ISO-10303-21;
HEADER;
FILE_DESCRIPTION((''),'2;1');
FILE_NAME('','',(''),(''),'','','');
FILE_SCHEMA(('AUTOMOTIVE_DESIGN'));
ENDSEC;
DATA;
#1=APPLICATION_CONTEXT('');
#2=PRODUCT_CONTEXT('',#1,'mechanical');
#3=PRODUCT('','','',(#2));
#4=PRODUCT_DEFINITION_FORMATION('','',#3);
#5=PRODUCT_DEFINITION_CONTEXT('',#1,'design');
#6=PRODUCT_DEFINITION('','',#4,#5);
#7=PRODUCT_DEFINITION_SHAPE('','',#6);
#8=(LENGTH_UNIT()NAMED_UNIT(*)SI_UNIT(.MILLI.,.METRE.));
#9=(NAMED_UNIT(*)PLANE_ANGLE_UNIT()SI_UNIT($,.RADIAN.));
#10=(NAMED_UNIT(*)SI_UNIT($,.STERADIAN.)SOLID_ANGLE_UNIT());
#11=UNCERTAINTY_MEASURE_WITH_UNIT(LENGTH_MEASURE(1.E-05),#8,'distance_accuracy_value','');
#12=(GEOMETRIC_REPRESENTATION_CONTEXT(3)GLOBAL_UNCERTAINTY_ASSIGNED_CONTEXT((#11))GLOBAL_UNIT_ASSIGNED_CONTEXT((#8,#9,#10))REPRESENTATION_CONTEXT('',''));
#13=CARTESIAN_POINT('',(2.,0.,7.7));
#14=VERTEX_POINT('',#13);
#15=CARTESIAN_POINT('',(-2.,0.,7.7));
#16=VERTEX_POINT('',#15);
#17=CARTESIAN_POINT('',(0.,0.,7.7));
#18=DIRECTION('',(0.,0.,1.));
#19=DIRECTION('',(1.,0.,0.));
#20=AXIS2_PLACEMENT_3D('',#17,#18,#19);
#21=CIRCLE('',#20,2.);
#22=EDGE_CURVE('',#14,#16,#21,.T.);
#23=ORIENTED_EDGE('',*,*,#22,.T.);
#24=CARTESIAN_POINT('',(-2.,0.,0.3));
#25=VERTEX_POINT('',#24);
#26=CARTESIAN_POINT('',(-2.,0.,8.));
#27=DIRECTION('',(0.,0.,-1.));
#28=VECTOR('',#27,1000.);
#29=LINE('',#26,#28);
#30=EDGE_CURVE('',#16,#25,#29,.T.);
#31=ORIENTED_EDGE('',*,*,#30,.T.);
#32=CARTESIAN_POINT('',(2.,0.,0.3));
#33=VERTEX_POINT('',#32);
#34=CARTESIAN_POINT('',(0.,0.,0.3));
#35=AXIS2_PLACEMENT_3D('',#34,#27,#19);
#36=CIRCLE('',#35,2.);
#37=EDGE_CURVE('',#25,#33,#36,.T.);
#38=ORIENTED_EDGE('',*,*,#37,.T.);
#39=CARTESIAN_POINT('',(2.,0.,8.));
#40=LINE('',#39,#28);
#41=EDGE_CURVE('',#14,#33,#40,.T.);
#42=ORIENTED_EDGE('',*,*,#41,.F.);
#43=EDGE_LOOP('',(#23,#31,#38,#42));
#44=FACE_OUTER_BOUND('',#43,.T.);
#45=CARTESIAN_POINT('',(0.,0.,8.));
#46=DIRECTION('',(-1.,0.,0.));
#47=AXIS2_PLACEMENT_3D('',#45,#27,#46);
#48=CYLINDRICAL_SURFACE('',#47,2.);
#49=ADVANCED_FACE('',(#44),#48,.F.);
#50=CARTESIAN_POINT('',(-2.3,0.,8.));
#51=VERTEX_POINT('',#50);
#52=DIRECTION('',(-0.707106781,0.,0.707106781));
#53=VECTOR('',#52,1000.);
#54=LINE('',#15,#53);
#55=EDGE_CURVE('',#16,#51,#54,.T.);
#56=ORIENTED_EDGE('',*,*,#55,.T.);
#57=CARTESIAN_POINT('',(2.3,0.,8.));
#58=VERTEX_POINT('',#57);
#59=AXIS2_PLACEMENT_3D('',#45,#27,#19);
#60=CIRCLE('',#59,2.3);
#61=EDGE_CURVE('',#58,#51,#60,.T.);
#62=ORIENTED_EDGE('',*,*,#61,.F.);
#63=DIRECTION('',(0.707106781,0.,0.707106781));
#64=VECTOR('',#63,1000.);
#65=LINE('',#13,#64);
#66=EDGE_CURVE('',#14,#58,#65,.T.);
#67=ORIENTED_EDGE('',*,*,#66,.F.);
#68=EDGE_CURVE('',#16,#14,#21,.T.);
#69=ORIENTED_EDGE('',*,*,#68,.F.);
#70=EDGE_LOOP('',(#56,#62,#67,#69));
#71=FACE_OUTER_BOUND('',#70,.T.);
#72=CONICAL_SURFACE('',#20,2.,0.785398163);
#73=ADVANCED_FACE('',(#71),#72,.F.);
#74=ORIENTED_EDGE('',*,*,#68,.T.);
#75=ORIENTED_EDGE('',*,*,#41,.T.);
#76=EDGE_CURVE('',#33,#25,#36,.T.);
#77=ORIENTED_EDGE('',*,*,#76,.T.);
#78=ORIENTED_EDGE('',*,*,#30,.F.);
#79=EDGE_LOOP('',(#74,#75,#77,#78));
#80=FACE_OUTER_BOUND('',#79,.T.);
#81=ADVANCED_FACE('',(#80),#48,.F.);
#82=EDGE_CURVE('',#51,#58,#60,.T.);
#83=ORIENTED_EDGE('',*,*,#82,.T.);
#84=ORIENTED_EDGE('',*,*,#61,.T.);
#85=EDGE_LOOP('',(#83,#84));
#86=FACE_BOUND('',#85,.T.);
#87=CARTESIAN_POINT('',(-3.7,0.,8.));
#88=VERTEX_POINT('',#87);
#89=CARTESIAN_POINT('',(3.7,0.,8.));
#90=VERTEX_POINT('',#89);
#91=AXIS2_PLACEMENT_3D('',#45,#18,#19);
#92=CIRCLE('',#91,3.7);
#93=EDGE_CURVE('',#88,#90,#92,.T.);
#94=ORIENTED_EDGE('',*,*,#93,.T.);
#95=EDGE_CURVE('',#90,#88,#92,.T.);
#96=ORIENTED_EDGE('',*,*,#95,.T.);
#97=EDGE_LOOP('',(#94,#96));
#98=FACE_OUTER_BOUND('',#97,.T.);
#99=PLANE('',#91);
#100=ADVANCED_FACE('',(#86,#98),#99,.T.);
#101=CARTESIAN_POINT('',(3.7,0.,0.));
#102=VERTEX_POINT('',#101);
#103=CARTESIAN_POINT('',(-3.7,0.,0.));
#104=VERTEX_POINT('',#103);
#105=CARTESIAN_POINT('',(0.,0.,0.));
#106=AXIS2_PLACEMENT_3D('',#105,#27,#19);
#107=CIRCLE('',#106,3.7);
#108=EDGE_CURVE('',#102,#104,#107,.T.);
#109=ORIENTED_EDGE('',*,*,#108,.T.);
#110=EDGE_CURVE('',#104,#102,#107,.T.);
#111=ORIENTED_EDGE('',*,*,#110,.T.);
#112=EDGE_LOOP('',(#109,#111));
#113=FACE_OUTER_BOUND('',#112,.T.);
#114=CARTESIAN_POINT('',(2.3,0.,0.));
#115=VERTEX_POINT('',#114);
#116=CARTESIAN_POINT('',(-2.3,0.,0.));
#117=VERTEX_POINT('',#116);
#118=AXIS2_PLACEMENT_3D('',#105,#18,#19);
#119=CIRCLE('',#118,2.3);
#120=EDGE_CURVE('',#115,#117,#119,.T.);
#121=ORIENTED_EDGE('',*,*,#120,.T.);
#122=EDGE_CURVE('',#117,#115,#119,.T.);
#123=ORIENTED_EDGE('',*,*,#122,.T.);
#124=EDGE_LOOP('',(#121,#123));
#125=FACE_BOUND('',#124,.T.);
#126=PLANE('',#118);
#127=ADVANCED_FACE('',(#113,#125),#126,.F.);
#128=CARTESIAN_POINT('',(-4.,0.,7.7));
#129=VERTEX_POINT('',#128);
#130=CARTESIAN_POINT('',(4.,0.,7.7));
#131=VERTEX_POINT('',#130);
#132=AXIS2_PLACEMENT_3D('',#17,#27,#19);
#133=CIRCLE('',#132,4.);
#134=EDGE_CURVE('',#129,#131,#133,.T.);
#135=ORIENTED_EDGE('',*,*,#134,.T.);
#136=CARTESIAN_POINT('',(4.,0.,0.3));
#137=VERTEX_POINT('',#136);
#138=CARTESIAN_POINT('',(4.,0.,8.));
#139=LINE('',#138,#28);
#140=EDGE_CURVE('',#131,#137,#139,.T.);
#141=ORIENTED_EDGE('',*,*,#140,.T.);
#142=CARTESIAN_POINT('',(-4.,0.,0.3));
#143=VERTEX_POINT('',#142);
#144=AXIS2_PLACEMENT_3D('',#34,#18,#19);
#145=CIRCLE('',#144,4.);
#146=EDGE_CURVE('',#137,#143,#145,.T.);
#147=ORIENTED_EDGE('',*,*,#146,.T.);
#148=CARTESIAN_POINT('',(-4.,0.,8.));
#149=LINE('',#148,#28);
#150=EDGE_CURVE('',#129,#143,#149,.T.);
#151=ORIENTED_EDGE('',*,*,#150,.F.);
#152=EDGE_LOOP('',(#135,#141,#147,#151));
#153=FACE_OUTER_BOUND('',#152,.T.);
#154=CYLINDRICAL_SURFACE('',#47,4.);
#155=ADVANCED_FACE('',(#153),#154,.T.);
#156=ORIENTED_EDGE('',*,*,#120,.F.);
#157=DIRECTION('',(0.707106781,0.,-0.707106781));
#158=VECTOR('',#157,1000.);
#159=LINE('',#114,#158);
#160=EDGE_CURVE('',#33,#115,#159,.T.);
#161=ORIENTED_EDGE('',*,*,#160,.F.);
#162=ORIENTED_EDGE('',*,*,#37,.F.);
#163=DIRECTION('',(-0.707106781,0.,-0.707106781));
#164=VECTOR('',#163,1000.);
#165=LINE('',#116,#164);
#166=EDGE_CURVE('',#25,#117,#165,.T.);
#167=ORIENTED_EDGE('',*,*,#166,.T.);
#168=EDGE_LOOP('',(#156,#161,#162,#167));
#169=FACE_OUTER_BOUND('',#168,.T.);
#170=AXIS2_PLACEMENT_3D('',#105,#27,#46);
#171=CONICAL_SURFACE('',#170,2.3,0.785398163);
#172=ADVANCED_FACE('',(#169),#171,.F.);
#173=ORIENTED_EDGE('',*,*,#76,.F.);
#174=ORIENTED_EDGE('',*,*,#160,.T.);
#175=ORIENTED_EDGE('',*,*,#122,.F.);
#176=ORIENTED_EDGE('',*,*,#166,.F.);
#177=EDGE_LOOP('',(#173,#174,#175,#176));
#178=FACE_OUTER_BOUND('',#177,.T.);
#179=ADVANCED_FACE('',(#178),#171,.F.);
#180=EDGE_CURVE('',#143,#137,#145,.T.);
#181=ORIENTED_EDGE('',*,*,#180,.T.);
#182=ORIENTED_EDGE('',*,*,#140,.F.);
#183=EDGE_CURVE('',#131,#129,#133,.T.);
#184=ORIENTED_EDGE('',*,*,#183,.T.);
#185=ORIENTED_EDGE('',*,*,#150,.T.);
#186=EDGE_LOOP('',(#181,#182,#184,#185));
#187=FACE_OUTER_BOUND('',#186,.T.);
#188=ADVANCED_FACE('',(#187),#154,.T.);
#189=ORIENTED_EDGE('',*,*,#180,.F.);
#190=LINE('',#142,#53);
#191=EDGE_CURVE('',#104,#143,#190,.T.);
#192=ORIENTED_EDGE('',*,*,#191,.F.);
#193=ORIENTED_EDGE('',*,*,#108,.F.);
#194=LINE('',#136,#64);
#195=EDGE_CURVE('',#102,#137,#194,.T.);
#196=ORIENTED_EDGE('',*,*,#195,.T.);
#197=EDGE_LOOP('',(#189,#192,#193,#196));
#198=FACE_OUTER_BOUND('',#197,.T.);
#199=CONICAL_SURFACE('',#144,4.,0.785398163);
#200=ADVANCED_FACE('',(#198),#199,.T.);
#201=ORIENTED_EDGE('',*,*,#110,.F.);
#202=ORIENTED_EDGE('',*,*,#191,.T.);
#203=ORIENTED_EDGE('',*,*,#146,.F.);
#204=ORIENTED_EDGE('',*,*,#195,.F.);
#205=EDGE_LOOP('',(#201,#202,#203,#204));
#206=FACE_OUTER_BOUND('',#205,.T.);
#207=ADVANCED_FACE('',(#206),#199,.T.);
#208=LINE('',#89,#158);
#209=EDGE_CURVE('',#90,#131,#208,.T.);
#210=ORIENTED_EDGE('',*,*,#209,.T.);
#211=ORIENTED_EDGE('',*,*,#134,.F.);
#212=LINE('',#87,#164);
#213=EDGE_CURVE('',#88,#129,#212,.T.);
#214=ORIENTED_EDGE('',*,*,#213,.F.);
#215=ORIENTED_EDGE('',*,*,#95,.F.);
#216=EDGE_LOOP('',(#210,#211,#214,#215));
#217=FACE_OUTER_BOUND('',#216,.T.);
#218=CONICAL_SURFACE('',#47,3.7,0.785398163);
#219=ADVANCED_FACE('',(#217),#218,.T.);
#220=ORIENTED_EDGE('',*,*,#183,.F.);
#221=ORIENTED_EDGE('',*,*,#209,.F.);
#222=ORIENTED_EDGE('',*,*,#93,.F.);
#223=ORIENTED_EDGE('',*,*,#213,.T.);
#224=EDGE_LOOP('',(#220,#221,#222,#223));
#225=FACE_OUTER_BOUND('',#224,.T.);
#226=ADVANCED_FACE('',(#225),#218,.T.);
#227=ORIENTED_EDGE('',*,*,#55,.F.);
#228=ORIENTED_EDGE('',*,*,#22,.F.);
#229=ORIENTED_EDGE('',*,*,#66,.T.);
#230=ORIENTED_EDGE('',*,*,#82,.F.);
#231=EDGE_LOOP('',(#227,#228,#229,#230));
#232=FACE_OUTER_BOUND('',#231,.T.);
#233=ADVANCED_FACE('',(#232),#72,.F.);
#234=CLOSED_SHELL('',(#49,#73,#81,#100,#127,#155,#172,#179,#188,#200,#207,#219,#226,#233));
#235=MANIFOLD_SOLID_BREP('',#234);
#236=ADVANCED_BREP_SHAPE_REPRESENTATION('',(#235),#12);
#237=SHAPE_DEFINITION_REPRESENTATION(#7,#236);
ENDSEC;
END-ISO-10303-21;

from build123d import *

# Parameters (mm, degrees)
SKETCH1_R           = 4
SKETCH1_R_2         = 2
BOSS_EXTRUDE1_DEPTH = 8
CHAMFER1_SIZE       = 0.3


with BuildPart() as part:
    # Sketch1 → Boss-Extrude1 (new body)
    with BuildSketch(Plane.XY):
        Circle(SKETCH1_R)
        Circle(SKETCH1_R_2, mode=Mode.SUBTRACT)
    extrude(amount=BOSS_EXTRUDE1_DEPTH)

    # Chamfer1
    chamfer1_edges = [part.edges().sort_by_distance(p)[0] for p in [
        (-4, 0, 0),
        (-4, 0, 8),
        (-2, 0, 0),
        (-2, 0, 8),
    ]]
    chamfer(chamfer1_edges, length=CHAMFER1_SIZE)


solid = part.part
